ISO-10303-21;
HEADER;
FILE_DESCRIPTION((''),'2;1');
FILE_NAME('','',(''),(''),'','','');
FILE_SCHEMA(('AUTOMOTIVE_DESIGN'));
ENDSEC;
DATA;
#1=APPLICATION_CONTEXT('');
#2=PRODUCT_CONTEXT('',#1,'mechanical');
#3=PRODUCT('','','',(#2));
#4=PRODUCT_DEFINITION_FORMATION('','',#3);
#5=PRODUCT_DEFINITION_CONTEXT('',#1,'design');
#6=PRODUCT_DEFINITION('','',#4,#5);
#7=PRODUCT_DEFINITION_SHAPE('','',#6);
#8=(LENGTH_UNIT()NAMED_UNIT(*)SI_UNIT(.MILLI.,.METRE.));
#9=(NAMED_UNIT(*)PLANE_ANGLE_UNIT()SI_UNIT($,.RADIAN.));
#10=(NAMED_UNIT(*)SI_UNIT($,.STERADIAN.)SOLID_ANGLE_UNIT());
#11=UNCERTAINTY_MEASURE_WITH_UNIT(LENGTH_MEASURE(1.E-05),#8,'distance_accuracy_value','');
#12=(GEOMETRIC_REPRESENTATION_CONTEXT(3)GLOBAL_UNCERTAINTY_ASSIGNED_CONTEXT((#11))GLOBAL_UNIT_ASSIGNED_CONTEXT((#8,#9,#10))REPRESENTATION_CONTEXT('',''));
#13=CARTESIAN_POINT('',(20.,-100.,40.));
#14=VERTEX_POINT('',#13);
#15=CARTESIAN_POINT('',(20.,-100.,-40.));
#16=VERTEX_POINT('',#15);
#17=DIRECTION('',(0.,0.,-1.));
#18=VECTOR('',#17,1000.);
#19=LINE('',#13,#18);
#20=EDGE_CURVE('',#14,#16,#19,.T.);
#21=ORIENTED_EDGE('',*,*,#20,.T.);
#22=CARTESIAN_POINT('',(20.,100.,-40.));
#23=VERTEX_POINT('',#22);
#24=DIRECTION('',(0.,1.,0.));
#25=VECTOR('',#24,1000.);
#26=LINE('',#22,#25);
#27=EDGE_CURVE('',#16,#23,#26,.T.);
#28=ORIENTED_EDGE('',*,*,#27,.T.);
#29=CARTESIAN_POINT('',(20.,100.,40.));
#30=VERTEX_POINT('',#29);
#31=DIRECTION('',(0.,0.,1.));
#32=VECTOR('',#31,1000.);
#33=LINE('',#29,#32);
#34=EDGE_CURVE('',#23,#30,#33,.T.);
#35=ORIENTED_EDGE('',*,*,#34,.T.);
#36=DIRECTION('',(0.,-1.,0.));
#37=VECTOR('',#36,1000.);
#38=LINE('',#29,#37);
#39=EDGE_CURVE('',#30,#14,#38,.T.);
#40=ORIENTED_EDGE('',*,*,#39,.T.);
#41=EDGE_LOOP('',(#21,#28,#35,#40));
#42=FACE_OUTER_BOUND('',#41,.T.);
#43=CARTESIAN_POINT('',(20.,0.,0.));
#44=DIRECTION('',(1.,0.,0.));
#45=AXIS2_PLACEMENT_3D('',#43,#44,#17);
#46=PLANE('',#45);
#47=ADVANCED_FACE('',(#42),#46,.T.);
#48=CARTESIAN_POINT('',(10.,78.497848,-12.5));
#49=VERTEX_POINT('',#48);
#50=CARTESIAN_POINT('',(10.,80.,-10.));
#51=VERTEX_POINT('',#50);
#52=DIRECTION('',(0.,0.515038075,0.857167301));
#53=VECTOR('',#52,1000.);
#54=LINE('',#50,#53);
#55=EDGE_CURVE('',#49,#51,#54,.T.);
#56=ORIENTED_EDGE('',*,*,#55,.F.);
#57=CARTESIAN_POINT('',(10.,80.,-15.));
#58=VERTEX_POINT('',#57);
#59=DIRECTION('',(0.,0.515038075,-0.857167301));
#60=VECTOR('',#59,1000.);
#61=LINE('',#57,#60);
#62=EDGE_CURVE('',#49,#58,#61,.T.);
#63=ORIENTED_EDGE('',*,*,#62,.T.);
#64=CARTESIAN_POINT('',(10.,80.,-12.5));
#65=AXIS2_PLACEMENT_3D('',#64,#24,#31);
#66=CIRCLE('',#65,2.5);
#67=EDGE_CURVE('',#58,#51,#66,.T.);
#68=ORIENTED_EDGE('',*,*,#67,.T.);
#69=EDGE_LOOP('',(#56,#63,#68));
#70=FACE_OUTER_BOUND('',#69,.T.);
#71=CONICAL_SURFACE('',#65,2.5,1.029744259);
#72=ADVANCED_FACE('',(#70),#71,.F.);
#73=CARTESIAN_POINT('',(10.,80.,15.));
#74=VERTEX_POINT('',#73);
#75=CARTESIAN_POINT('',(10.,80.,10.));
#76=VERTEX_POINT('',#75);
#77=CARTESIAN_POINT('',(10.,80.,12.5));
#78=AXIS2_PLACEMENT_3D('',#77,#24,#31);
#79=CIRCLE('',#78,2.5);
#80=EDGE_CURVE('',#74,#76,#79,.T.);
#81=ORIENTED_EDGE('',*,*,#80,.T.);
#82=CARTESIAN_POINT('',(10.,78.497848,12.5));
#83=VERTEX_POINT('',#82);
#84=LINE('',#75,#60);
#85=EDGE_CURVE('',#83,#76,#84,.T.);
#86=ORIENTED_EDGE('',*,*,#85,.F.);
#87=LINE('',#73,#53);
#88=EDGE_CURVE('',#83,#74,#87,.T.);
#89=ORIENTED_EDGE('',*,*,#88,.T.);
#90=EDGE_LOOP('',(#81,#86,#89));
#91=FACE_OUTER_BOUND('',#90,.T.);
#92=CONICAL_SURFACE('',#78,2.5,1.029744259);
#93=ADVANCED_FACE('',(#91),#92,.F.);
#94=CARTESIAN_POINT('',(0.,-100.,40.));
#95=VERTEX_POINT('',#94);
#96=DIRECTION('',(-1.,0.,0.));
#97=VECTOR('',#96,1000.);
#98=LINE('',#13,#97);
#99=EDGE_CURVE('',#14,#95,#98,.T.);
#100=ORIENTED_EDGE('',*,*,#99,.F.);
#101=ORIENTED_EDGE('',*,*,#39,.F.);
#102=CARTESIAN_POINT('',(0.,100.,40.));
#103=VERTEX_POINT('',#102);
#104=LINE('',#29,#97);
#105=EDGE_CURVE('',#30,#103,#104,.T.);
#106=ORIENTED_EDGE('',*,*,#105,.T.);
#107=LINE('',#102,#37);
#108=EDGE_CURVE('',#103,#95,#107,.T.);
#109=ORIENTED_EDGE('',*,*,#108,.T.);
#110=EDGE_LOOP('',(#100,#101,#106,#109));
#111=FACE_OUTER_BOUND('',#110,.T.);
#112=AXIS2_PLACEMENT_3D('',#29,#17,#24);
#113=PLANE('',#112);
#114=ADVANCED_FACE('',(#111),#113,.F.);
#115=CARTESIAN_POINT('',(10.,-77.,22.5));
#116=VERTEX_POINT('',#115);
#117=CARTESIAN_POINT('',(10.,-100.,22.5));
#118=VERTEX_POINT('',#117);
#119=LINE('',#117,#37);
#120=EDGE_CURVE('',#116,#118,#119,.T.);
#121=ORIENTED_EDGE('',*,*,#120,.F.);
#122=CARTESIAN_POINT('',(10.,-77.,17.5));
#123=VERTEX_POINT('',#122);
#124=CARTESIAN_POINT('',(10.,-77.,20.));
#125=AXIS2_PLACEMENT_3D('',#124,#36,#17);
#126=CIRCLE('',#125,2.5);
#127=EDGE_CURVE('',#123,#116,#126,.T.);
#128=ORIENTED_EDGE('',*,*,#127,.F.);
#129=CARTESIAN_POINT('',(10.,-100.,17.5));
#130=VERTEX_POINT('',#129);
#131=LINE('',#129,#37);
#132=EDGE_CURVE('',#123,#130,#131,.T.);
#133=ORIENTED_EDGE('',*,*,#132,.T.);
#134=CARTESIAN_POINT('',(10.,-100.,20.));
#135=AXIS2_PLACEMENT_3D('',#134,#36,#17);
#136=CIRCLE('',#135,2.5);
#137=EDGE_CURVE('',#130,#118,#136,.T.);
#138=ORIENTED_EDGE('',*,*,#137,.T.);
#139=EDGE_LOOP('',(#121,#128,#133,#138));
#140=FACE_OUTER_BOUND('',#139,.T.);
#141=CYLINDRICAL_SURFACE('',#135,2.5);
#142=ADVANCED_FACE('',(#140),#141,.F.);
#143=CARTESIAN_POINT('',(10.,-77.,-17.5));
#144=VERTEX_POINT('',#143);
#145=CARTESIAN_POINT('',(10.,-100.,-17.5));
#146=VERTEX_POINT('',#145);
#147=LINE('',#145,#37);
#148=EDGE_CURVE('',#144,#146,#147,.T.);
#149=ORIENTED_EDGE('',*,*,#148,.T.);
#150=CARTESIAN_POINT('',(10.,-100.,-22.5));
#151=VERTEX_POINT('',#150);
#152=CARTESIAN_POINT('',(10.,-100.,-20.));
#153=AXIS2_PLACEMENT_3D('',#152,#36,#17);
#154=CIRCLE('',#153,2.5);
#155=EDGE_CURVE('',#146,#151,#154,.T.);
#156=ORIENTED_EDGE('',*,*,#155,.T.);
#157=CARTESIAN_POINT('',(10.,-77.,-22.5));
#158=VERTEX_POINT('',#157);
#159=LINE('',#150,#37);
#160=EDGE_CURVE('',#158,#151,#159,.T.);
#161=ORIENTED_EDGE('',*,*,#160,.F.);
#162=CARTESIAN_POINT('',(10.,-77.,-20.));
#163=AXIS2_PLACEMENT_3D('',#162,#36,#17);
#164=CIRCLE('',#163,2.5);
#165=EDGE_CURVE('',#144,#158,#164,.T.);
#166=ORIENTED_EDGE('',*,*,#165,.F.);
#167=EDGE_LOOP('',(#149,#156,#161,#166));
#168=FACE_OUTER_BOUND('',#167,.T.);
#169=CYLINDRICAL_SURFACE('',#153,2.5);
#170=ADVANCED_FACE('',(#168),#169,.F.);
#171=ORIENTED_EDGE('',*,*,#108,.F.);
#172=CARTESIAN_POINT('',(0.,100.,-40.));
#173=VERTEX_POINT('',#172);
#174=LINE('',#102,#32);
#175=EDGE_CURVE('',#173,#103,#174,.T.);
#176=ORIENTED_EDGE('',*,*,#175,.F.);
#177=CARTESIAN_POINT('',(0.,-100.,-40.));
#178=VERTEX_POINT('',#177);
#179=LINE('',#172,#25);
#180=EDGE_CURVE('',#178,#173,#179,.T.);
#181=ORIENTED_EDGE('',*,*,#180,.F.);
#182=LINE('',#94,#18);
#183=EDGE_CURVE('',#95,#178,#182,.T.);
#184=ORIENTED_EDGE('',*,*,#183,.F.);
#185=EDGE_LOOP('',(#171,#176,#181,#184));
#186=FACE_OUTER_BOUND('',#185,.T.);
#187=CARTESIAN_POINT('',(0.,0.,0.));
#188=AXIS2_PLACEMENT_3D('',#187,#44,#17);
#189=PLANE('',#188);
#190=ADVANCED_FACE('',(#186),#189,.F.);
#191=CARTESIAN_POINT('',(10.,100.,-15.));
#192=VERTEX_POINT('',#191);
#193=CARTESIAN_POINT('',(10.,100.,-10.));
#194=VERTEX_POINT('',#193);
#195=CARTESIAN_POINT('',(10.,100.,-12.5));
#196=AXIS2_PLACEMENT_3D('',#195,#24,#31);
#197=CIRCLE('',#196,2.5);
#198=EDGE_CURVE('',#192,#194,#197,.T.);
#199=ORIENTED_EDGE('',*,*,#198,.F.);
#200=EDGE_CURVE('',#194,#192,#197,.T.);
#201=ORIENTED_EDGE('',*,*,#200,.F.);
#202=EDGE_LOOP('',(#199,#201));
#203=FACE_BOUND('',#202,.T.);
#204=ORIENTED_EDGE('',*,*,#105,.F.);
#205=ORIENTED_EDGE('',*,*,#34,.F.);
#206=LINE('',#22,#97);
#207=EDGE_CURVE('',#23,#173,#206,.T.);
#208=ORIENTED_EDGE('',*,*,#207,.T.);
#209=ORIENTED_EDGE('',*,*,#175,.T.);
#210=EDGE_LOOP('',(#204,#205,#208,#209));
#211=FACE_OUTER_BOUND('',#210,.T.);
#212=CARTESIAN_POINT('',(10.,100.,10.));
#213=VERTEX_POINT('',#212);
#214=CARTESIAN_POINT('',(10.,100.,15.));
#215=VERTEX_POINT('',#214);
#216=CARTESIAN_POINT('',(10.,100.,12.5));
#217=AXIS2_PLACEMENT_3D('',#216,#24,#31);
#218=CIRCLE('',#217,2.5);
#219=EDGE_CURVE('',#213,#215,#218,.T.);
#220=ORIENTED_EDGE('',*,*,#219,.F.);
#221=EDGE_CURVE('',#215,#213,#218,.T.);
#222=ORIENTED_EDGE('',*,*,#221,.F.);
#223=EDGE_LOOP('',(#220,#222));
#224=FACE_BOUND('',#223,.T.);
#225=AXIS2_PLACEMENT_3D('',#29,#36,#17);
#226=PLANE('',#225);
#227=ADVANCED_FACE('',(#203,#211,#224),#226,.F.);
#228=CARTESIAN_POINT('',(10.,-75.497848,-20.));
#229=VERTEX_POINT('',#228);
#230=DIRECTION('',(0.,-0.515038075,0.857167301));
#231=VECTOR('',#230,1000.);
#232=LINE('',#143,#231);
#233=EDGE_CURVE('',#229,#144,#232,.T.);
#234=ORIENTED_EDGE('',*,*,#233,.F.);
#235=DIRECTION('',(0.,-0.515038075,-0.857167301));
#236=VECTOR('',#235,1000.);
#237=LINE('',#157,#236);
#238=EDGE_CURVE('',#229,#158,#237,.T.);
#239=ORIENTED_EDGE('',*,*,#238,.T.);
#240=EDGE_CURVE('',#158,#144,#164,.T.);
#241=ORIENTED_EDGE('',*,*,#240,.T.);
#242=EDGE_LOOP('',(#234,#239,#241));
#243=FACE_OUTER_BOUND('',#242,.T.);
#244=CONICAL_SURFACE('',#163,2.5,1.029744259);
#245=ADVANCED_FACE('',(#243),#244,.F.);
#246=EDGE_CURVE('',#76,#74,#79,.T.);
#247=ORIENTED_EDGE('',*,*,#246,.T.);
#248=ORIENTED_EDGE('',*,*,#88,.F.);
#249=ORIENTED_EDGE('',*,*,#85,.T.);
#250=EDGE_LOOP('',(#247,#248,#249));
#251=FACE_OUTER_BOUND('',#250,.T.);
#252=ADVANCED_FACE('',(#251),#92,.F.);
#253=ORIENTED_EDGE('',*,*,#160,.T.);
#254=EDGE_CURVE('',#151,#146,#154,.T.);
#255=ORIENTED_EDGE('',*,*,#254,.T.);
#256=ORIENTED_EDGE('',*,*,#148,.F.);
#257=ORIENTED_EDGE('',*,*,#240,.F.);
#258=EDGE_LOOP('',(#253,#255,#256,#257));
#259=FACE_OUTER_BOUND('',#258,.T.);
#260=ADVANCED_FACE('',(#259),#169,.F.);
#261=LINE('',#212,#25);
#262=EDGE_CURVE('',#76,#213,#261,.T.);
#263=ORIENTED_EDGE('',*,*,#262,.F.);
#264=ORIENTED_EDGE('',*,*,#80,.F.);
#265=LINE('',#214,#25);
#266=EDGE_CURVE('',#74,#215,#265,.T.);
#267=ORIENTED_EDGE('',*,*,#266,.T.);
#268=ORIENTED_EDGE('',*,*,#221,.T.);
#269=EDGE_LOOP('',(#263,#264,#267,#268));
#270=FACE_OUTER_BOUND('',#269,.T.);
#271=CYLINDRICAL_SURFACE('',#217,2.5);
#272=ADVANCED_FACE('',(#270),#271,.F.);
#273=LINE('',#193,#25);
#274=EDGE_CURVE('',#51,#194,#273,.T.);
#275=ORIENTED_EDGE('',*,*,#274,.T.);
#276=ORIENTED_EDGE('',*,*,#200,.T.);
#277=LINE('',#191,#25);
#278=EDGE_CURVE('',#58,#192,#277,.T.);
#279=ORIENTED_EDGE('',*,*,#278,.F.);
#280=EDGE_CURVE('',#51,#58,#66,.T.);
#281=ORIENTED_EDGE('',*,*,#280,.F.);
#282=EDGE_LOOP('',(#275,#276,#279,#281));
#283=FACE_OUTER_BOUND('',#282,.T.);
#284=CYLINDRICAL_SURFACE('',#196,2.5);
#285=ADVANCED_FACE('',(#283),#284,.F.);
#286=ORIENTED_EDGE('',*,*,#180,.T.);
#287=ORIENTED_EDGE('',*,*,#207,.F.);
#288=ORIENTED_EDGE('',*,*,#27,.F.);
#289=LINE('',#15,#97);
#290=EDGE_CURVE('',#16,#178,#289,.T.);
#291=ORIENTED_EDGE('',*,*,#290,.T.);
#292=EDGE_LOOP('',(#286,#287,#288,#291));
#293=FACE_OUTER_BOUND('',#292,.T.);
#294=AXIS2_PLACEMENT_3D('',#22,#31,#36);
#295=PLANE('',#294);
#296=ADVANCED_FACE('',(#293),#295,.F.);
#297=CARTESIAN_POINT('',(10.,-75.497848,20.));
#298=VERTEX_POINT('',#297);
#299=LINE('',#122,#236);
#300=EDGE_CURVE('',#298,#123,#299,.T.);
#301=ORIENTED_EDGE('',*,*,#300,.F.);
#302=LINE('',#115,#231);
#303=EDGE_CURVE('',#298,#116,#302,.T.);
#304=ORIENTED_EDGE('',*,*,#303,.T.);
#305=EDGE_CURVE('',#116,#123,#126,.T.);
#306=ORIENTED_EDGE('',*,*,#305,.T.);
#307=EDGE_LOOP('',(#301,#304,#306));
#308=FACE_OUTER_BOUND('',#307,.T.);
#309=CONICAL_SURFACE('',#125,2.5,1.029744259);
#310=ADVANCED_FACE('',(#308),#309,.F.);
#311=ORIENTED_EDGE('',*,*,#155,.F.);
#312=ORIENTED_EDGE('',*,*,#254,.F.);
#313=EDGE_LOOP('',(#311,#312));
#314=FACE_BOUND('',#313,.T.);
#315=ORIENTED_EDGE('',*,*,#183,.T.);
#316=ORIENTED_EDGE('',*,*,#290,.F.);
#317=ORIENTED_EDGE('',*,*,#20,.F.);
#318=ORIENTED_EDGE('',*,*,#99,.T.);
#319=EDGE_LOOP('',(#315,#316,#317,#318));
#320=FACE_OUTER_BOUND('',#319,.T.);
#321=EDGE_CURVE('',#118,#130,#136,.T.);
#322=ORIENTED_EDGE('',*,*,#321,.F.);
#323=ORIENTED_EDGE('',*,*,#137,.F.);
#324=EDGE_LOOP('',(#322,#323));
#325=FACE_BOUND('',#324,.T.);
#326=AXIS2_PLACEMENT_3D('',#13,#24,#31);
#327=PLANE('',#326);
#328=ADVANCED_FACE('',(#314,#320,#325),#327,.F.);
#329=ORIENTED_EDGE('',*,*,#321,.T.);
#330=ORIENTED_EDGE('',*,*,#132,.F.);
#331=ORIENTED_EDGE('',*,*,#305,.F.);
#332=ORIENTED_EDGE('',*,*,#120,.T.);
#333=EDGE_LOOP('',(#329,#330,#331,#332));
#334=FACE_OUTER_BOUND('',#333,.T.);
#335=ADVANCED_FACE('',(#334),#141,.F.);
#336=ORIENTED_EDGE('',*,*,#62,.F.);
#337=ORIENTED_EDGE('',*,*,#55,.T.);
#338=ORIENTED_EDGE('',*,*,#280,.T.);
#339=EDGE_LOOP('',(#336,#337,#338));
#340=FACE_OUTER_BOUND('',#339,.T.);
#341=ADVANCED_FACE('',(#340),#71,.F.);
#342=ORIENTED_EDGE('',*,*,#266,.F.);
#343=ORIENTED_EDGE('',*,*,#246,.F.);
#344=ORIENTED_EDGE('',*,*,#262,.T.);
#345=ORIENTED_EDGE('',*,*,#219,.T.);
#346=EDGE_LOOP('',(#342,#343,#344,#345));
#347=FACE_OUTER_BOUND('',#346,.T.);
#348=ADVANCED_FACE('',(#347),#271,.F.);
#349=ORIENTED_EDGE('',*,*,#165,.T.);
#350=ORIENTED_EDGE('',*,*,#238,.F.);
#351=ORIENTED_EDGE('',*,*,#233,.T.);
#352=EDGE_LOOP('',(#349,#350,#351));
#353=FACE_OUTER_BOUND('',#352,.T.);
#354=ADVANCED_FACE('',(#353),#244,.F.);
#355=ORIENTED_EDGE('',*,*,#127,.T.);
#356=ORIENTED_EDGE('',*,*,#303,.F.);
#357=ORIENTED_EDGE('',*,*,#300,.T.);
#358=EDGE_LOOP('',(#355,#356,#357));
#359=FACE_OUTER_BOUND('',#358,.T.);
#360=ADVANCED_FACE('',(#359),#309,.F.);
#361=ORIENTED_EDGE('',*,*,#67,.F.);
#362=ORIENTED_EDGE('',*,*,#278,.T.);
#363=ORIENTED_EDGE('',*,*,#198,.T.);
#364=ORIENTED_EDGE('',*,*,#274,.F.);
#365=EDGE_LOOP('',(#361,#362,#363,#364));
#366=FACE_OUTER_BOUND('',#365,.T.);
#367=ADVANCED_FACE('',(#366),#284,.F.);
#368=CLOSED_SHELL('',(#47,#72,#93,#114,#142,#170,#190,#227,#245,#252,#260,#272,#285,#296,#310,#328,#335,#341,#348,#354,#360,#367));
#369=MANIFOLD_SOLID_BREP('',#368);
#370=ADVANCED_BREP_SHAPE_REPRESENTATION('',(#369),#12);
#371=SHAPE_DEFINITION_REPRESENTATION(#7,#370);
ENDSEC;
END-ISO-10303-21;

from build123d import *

# Parameters (mm, degrees)
SKETCH_1_W             = 80
SKETCH_1_H             = 200
EXTRUDE_1_DEPTH        = 20
HOLE_WIZARD_M6_1_D     = 5
HOLE_WIZARD_M6_1_DEPTH = 20
HOLE_WIZARD_M6_1_TIP   = 1.502151548
HOLE_WIZARD_M6_2_D     = 5
HOLE_WIZARD_M6_2_DEPTH = 23
HOLE_WIZARD_M6_2_TIP   = 1.502151548


with BuildPart() as part:
    # 草图1 → 凸台-拉伸1 (new body)
    with BuildSketch(Plane(origin=(0, 0, 0), x_dir=(0, 0, -1), z_dir=(1, 0, 0))):
        Rectangle(SKETCH_1_W, SKETCH_1_H)
    extrude(amount=EXTRUDE_1_DEPTH)

    # M6 螺纹孔1
    with Locations(Plane(origin=(0, 100, 0), x_dir=(1, 0, 0), z_dir=(0, 1, 0))):
        with Locations((10, 12.5), (10, -12.5)):
            Hole(HOLE_WIZARD_M6_1_D / 2, depth=HOLE_WIZARD_M6_1_DEPTH)
            with Locations((0, 0, -(HOLE_WIZARD_M6_1_DEPTH + HOLE_WIZARD_M6_1_TIP / 2))):  # 118° drill point
                Cone(0, HOLE_WIZARD_M6_1_D / 2, HOLE_WIZARD_M6_1_TIP, mode=Mode.SUBTRACT)

    # M6 螺纹孔2
    with Locations(Plane(origin=(0, -100, 0), x_dir=(-1, 0, 0), z_dir=(0, -1, 0))):
        with Locations((-10, 20), (-10, -20)):
            Hole(HOLE_WIZARD_M6_2_D / 2, depth=HOLE_WIZARD_M6_2_DEPTH)
            with Locations((0, 0, -(HOLE_WIZARD_M6_2_DEPTH + HOLE_WIZARD_M6_2_TIP / 2))):  # 118° drill point
                Cone(0, HOLE_WIZARD_M6_2_D / 2, HOLE_WIZARD_M6_2_TIP, mode=Mode.SUBTRACT)


solid = part.part
